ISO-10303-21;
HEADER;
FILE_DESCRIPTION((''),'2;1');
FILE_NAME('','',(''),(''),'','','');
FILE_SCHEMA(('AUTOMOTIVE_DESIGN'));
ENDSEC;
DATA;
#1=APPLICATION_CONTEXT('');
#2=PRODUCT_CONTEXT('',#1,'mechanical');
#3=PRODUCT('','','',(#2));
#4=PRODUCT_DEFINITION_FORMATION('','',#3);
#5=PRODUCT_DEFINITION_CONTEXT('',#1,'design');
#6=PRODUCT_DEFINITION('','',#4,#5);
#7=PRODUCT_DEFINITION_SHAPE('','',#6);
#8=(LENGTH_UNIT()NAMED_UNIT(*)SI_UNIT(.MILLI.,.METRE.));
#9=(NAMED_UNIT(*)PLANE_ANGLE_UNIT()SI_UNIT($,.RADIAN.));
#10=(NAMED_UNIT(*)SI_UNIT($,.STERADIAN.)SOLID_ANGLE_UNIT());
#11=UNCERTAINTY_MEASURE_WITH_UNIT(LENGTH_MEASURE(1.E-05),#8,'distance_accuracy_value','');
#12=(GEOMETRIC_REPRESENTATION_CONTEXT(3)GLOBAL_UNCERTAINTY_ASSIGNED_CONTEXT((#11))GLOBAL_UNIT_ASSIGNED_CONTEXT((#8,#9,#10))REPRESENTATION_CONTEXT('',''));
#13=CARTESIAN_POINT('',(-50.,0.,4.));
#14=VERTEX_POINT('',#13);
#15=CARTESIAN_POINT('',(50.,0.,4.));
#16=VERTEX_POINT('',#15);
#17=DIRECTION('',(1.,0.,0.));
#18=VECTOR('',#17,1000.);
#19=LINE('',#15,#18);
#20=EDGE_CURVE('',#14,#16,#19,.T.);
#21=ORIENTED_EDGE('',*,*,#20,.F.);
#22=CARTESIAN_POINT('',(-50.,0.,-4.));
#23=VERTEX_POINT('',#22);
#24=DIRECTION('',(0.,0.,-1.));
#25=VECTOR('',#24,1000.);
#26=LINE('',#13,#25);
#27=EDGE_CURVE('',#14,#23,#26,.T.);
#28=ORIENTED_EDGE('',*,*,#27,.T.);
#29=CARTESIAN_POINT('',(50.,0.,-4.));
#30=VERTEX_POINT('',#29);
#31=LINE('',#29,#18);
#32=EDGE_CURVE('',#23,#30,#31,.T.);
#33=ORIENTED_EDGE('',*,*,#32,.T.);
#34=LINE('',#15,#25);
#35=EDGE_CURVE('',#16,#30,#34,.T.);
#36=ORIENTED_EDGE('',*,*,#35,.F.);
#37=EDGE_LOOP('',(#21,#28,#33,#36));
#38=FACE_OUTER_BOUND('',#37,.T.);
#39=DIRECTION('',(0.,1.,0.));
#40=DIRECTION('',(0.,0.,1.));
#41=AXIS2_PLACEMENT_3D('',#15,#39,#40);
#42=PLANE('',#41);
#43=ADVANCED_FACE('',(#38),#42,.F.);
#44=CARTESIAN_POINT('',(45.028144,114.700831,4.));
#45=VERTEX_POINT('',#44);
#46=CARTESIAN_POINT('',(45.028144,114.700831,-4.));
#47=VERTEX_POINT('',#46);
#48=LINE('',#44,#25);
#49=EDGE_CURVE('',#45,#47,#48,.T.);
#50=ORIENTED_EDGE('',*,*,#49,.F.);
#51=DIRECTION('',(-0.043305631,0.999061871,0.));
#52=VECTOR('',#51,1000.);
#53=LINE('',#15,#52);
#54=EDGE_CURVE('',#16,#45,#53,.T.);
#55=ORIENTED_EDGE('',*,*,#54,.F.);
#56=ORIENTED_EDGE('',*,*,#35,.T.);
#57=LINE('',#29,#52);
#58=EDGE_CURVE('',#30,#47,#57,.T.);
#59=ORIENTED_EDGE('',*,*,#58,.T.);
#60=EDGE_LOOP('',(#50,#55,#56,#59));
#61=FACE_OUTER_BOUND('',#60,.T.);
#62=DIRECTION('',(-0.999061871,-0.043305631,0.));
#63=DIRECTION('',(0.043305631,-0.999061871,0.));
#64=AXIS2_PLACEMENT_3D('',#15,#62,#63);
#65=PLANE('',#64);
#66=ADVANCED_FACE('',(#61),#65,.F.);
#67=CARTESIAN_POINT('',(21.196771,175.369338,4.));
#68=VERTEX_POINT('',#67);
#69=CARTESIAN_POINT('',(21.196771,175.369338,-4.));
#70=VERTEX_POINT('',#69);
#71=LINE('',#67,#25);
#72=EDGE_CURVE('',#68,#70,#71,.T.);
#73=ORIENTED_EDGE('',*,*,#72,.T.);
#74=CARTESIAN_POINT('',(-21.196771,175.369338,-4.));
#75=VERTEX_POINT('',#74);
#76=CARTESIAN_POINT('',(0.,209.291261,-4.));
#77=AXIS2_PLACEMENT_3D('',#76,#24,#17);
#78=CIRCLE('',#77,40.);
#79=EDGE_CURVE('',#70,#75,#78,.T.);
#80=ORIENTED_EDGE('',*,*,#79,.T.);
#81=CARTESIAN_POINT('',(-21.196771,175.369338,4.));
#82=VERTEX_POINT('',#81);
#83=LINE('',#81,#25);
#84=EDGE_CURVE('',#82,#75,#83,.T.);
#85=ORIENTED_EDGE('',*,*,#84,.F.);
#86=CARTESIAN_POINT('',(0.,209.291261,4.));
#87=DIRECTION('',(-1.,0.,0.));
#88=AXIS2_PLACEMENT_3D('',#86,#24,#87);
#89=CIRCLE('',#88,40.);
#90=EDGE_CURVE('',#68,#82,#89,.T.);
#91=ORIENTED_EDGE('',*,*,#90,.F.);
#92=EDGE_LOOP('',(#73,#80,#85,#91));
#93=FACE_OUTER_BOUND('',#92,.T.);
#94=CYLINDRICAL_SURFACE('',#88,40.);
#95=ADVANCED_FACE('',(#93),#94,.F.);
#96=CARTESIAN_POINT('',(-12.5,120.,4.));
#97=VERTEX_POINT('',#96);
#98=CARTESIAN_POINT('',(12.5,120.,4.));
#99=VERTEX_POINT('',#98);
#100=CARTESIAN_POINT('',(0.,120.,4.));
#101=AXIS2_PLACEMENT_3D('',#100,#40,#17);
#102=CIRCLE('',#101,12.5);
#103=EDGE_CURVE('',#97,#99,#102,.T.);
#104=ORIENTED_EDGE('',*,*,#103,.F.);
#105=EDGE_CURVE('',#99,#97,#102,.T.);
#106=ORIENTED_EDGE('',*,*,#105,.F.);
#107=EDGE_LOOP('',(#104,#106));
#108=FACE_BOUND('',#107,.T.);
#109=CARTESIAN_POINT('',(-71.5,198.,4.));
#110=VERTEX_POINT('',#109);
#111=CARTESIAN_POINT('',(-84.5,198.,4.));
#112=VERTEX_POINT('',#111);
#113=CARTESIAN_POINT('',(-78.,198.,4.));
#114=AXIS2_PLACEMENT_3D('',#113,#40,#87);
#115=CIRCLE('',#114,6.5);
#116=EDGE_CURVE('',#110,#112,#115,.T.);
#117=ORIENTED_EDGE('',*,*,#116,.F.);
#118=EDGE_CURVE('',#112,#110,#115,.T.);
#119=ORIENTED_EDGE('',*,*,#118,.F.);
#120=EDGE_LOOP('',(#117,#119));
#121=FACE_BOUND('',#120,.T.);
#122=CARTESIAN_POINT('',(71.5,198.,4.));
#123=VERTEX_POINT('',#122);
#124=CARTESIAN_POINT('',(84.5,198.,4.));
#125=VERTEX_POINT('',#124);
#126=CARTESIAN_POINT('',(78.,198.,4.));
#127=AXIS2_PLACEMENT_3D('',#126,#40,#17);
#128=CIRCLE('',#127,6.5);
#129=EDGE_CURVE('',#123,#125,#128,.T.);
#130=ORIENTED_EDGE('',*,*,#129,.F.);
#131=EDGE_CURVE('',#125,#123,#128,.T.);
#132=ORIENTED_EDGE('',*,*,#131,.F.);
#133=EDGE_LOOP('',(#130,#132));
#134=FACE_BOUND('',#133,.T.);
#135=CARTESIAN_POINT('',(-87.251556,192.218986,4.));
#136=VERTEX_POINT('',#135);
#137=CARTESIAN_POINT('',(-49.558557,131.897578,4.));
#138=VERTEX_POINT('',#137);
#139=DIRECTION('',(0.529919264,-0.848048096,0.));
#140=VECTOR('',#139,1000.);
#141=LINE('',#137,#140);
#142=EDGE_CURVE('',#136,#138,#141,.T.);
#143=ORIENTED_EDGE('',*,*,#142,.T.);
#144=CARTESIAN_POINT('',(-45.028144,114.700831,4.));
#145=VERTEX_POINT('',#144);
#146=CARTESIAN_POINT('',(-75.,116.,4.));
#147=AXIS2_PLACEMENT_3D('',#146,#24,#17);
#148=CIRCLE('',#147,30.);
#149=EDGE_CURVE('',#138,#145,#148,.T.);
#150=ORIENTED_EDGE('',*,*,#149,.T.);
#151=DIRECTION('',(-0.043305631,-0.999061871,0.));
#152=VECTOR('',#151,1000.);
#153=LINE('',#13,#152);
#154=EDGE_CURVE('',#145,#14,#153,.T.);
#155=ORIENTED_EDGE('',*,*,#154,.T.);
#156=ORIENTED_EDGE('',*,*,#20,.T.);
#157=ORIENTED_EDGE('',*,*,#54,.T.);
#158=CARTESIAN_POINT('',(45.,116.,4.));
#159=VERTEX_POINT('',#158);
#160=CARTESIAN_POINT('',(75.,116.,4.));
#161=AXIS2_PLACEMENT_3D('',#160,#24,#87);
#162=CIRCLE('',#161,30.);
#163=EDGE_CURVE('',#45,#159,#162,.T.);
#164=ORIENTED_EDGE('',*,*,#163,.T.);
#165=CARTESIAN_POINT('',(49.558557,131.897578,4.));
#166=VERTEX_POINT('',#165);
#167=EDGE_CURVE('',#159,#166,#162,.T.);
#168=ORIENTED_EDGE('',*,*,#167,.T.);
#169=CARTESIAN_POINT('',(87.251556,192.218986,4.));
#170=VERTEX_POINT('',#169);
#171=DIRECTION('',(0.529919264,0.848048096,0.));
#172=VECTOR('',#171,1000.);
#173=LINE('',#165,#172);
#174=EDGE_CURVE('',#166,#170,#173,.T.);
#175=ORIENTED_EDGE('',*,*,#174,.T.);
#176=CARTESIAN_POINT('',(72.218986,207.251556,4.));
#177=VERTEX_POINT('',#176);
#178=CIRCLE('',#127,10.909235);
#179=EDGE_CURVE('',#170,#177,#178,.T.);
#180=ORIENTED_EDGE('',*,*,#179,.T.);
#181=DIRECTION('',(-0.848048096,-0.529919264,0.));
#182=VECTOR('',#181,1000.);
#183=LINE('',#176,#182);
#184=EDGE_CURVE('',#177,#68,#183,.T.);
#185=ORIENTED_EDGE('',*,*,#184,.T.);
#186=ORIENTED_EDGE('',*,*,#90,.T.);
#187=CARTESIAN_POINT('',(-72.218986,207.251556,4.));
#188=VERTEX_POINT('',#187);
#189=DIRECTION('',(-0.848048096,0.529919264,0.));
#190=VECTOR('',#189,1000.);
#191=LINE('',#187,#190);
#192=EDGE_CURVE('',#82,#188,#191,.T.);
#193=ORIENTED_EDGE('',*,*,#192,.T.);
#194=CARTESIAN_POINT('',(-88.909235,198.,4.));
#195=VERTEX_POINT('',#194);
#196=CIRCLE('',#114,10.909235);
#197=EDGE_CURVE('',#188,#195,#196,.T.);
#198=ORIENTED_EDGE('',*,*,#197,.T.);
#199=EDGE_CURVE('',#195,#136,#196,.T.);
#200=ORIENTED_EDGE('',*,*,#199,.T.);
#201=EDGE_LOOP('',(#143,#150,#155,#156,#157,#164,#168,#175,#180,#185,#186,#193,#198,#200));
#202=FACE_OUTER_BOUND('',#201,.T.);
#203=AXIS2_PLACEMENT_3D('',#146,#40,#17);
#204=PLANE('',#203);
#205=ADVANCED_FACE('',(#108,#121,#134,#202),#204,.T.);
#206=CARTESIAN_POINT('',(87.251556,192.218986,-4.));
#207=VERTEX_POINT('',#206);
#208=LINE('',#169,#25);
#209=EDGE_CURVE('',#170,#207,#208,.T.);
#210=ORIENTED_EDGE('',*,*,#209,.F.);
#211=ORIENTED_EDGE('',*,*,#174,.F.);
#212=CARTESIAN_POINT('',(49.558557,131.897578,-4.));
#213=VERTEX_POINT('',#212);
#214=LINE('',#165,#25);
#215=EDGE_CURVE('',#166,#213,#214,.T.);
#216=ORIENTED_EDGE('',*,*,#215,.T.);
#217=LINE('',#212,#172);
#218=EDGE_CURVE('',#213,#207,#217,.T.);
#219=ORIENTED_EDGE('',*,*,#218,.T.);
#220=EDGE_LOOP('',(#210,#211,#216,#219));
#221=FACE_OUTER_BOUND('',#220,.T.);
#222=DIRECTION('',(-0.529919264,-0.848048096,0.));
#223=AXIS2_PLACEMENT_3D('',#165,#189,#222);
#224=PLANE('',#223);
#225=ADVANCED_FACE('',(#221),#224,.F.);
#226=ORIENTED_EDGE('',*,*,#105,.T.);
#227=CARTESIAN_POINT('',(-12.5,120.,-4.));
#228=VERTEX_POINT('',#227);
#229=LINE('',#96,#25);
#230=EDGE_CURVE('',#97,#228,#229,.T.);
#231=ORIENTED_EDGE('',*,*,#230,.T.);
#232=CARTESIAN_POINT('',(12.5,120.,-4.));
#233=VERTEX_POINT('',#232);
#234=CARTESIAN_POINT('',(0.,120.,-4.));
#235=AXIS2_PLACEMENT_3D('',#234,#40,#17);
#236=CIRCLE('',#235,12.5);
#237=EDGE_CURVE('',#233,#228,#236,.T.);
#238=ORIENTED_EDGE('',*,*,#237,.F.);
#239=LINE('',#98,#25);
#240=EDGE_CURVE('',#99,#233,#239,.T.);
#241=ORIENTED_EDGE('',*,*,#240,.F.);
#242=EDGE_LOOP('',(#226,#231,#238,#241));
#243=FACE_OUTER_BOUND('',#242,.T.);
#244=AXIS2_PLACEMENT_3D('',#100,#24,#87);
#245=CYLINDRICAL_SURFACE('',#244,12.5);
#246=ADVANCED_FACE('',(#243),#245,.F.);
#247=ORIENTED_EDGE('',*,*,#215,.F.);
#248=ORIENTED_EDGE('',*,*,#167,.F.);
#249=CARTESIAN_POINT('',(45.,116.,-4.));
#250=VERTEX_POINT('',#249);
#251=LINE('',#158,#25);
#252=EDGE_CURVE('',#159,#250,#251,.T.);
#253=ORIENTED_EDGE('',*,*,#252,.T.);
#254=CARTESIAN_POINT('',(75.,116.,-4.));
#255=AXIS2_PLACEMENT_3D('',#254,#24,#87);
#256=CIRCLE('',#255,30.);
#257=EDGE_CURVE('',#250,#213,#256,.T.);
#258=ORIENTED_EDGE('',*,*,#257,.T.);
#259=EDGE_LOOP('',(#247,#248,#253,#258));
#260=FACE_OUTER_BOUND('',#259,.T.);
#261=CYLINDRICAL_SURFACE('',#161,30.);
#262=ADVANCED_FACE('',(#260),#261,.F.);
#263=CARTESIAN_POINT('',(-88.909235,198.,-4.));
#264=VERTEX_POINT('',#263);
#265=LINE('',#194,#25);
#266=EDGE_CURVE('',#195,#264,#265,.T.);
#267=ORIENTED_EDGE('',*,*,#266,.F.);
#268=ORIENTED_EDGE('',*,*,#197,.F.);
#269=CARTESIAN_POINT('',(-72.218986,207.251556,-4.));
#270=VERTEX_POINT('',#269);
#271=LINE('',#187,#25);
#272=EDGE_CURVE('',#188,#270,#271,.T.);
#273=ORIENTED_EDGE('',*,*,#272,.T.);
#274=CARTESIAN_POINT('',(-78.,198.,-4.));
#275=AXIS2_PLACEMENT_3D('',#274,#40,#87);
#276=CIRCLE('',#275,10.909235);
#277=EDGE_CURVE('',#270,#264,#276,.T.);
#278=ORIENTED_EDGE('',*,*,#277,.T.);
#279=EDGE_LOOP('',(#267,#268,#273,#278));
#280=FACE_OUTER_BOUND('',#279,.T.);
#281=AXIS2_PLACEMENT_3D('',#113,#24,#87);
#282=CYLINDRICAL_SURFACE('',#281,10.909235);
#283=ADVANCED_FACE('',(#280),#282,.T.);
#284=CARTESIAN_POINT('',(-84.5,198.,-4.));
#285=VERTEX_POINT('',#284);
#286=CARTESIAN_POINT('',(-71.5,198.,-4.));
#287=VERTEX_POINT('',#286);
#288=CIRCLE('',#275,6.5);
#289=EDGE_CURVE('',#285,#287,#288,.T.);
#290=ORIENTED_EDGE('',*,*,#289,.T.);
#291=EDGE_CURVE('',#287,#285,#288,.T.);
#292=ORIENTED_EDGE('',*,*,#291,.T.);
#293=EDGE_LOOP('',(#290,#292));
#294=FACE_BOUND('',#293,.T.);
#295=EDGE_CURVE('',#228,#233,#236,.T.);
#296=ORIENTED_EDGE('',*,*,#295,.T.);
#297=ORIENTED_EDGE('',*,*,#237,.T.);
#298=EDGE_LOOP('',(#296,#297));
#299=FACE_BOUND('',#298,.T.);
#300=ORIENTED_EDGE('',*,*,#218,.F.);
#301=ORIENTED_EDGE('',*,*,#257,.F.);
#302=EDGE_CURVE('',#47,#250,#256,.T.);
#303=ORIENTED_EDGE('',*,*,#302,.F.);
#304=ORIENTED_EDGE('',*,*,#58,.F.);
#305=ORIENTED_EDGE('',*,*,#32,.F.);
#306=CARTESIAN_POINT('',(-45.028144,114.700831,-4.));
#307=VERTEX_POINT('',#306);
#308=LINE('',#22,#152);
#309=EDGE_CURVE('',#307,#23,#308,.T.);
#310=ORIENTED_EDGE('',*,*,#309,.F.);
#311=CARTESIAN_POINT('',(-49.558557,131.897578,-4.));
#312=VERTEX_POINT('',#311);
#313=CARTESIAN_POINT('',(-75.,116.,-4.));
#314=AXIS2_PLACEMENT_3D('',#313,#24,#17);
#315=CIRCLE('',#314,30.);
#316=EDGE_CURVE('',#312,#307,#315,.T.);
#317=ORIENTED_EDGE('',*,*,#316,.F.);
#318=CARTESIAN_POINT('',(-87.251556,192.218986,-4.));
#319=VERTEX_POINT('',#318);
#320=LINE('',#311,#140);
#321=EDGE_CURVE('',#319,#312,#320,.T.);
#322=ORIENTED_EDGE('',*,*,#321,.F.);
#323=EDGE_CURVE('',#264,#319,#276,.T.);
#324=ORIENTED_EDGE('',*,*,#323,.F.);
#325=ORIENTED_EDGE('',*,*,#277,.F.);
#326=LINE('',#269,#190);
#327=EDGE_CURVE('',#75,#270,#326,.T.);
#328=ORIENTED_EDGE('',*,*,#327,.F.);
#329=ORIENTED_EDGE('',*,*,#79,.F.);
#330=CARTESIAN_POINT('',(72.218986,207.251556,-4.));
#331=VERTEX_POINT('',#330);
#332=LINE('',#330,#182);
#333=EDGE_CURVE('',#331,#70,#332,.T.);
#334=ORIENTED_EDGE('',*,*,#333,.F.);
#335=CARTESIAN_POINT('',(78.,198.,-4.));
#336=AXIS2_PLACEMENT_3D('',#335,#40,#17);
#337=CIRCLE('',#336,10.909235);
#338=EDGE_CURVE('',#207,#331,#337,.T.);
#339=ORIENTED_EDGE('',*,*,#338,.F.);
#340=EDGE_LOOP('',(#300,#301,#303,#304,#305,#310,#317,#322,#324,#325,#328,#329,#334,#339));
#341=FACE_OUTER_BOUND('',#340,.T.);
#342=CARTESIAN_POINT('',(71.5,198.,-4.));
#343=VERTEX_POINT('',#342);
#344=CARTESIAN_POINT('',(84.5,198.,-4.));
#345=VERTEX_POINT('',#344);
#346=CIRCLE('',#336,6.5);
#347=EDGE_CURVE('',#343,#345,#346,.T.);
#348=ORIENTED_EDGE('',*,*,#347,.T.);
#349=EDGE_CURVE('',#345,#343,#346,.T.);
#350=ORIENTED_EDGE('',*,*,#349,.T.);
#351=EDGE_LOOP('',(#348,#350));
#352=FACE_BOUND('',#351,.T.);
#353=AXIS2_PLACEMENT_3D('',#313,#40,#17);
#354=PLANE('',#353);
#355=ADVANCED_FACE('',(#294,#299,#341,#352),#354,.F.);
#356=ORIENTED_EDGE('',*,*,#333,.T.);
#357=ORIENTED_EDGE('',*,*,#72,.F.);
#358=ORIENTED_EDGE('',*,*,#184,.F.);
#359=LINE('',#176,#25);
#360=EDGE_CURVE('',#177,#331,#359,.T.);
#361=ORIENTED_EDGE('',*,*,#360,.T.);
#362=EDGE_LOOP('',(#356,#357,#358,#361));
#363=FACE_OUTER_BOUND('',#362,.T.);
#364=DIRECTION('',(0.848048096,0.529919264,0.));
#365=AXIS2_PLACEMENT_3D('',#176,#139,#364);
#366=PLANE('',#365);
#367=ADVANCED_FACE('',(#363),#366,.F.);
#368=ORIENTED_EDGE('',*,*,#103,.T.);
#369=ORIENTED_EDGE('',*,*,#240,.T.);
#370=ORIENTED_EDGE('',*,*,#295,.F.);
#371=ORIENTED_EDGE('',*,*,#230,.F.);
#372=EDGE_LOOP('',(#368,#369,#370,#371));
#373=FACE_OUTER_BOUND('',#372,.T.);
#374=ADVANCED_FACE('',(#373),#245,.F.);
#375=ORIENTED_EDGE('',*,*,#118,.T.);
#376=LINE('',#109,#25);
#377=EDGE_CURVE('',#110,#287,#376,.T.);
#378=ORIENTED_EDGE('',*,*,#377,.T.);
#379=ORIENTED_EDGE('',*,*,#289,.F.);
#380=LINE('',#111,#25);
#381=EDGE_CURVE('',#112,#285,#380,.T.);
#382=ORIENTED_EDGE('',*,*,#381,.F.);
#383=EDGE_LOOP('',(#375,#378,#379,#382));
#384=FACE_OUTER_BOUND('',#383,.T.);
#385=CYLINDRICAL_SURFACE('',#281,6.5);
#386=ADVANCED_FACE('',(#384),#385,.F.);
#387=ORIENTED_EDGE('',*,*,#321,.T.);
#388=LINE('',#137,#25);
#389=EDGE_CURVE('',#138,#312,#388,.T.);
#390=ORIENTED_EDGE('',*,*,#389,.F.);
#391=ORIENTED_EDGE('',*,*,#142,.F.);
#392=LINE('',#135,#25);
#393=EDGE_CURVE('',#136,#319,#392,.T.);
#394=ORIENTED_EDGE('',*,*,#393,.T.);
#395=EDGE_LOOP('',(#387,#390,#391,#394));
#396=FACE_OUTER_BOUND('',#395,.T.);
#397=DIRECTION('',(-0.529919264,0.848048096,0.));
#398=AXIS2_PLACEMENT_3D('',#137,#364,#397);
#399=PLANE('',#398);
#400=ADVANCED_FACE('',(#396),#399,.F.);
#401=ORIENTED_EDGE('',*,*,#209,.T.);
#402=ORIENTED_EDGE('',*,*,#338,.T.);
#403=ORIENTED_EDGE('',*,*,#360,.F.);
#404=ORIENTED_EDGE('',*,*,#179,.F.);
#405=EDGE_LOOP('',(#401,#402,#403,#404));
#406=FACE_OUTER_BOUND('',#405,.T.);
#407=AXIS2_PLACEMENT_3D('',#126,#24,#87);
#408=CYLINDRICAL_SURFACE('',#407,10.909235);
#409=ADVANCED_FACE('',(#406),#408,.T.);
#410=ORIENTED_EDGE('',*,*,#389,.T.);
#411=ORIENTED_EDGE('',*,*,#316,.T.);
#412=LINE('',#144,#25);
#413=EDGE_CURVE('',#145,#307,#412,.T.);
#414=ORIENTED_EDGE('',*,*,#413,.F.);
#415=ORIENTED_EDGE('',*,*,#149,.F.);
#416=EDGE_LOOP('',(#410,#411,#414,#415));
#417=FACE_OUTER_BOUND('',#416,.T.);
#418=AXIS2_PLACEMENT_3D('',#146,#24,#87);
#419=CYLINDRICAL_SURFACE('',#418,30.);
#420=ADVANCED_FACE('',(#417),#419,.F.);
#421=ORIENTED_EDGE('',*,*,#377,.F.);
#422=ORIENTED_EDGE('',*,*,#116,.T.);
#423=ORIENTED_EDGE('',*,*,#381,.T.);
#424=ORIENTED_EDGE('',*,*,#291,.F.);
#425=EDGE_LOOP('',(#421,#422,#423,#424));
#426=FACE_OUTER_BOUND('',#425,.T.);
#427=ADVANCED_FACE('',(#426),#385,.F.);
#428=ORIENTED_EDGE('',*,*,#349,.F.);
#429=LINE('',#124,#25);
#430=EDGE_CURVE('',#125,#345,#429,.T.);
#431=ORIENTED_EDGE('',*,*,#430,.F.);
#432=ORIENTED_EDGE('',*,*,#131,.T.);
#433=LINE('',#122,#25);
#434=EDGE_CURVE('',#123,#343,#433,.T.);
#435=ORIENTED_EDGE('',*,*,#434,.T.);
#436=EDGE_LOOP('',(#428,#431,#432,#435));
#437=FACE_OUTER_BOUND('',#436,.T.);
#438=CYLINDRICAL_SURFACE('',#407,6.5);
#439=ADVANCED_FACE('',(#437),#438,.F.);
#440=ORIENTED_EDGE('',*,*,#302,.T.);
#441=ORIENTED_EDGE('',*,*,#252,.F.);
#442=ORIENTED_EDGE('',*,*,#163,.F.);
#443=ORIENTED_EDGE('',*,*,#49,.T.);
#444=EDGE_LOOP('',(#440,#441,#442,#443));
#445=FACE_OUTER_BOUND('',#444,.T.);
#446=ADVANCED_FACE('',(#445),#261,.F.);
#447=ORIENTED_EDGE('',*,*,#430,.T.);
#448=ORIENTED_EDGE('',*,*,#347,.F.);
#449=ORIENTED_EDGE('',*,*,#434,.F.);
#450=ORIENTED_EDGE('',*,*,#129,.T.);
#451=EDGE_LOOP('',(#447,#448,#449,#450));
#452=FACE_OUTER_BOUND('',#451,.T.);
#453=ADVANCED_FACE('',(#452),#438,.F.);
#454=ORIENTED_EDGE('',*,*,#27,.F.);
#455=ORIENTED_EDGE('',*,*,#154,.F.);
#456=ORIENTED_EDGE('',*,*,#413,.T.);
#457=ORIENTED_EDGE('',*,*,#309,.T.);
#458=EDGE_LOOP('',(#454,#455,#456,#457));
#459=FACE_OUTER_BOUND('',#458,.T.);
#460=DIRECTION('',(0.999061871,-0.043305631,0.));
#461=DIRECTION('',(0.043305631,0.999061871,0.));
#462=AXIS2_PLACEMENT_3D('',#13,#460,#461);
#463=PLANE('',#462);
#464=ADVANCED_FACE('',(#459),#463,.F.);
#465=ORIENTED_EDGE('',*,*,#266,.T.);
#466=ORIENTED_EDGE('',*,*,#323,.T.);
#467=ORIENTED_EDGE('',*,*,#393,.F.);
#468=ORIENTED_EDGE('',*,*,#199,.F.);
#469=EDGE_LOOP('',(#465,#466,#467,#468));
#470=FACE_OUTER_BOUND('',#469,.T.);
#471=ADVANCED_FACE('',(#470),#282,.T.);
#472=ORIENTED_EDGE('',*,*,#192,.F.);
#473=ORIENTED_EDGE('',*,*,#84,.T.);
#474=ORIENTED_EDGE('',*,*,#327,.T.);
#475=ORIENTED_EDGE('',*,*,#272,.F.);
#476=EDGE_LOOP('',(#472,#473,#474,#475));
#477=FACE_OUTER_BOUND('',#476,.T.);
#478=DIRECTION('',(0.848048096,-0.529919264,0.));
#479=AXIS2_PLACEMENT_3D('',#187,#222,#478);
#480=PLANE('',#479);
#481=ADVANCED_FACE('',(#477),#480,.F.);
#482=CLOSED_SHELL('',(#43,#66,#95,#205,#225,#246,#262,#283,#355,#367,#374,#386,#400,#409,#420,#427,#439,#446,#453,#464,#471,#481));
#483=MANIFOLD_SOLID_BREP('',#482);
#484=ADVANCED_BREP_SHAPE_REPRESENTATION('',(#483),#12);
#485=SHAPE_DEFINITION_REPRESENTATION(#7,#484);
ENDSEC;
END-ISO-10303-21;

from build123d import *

# Parameters (mm, degrees)
SKETCH1_R           = 12.5
SKETCH1_R_2         = 6.5
BOSS_EXTRUDE1_DEPTH = 4


with BuildPart() as part:
    # Sketch1 → Boss-Extrude1 (new, symmetric)
    with BuildSketch(Plane.XY):
        with BuildLine():
            Line((50, 0), (-50, 0))
            Line((-50, 0), (-45.028143867, 114.700831063))
            ThreePointArc((-45.028143867, 114.700831063), (-45.989821567, 123.642613906), (-49.558557115, 131.897577927))
            Line((-49.558557115, 131.897577927), (-87.251556293, 192.218986015))
            ThreePointArc((-87.251556293, 192.218986015), (-85.713994314, 205.713994314), (-72.218986015, 207.251556293))
            Line((-72.218986015, 207.251556293), (-21.196770569, 175.369337595))
            ThreePointArc((-21.196770569, 175.369337595), (-11.025494233, 170.840793604), (0, 169.291261441))
            ThreePointArc((0, 169.291261441), (11.025494233, 170.840793604), (21.196770569, 175.369337595))
            Line((21.196770569, 175.369337595), (72.218986015, 207.251556293))
            ThreePointArc((72.218986015, 207.251556293), (85.713994314, 205.713994314), (87.251556293, 192.218986015))
            Line((87.251556293, 192.218986015), (49.558557115, 131.897577927))
            ThreePointArc((49.558557115, 131.897577927), (45.989821567, 123.642613906), (45.028143867, 114.700831063))
            Line((45.028143867, 114.700831063), (50, 0))
        make_face()
        with Locations((0, 120)):
            Circle(SKETCH1_R, mode=Mode.SUBTRACT)
        with Locations((78, 198)):
            Circle(SKETCH1_R_2, mode=Mode.SUBTRACT)
        with Locations(Location((-78, 198, 0), (0, 0, 180))):
            Circle(SKETCH1_R_2, mode=Mode.SUBTRACT)
    extrude(amount=BOSS_EXTRUDE1_DEPTH, both=True)


solid = part.part
